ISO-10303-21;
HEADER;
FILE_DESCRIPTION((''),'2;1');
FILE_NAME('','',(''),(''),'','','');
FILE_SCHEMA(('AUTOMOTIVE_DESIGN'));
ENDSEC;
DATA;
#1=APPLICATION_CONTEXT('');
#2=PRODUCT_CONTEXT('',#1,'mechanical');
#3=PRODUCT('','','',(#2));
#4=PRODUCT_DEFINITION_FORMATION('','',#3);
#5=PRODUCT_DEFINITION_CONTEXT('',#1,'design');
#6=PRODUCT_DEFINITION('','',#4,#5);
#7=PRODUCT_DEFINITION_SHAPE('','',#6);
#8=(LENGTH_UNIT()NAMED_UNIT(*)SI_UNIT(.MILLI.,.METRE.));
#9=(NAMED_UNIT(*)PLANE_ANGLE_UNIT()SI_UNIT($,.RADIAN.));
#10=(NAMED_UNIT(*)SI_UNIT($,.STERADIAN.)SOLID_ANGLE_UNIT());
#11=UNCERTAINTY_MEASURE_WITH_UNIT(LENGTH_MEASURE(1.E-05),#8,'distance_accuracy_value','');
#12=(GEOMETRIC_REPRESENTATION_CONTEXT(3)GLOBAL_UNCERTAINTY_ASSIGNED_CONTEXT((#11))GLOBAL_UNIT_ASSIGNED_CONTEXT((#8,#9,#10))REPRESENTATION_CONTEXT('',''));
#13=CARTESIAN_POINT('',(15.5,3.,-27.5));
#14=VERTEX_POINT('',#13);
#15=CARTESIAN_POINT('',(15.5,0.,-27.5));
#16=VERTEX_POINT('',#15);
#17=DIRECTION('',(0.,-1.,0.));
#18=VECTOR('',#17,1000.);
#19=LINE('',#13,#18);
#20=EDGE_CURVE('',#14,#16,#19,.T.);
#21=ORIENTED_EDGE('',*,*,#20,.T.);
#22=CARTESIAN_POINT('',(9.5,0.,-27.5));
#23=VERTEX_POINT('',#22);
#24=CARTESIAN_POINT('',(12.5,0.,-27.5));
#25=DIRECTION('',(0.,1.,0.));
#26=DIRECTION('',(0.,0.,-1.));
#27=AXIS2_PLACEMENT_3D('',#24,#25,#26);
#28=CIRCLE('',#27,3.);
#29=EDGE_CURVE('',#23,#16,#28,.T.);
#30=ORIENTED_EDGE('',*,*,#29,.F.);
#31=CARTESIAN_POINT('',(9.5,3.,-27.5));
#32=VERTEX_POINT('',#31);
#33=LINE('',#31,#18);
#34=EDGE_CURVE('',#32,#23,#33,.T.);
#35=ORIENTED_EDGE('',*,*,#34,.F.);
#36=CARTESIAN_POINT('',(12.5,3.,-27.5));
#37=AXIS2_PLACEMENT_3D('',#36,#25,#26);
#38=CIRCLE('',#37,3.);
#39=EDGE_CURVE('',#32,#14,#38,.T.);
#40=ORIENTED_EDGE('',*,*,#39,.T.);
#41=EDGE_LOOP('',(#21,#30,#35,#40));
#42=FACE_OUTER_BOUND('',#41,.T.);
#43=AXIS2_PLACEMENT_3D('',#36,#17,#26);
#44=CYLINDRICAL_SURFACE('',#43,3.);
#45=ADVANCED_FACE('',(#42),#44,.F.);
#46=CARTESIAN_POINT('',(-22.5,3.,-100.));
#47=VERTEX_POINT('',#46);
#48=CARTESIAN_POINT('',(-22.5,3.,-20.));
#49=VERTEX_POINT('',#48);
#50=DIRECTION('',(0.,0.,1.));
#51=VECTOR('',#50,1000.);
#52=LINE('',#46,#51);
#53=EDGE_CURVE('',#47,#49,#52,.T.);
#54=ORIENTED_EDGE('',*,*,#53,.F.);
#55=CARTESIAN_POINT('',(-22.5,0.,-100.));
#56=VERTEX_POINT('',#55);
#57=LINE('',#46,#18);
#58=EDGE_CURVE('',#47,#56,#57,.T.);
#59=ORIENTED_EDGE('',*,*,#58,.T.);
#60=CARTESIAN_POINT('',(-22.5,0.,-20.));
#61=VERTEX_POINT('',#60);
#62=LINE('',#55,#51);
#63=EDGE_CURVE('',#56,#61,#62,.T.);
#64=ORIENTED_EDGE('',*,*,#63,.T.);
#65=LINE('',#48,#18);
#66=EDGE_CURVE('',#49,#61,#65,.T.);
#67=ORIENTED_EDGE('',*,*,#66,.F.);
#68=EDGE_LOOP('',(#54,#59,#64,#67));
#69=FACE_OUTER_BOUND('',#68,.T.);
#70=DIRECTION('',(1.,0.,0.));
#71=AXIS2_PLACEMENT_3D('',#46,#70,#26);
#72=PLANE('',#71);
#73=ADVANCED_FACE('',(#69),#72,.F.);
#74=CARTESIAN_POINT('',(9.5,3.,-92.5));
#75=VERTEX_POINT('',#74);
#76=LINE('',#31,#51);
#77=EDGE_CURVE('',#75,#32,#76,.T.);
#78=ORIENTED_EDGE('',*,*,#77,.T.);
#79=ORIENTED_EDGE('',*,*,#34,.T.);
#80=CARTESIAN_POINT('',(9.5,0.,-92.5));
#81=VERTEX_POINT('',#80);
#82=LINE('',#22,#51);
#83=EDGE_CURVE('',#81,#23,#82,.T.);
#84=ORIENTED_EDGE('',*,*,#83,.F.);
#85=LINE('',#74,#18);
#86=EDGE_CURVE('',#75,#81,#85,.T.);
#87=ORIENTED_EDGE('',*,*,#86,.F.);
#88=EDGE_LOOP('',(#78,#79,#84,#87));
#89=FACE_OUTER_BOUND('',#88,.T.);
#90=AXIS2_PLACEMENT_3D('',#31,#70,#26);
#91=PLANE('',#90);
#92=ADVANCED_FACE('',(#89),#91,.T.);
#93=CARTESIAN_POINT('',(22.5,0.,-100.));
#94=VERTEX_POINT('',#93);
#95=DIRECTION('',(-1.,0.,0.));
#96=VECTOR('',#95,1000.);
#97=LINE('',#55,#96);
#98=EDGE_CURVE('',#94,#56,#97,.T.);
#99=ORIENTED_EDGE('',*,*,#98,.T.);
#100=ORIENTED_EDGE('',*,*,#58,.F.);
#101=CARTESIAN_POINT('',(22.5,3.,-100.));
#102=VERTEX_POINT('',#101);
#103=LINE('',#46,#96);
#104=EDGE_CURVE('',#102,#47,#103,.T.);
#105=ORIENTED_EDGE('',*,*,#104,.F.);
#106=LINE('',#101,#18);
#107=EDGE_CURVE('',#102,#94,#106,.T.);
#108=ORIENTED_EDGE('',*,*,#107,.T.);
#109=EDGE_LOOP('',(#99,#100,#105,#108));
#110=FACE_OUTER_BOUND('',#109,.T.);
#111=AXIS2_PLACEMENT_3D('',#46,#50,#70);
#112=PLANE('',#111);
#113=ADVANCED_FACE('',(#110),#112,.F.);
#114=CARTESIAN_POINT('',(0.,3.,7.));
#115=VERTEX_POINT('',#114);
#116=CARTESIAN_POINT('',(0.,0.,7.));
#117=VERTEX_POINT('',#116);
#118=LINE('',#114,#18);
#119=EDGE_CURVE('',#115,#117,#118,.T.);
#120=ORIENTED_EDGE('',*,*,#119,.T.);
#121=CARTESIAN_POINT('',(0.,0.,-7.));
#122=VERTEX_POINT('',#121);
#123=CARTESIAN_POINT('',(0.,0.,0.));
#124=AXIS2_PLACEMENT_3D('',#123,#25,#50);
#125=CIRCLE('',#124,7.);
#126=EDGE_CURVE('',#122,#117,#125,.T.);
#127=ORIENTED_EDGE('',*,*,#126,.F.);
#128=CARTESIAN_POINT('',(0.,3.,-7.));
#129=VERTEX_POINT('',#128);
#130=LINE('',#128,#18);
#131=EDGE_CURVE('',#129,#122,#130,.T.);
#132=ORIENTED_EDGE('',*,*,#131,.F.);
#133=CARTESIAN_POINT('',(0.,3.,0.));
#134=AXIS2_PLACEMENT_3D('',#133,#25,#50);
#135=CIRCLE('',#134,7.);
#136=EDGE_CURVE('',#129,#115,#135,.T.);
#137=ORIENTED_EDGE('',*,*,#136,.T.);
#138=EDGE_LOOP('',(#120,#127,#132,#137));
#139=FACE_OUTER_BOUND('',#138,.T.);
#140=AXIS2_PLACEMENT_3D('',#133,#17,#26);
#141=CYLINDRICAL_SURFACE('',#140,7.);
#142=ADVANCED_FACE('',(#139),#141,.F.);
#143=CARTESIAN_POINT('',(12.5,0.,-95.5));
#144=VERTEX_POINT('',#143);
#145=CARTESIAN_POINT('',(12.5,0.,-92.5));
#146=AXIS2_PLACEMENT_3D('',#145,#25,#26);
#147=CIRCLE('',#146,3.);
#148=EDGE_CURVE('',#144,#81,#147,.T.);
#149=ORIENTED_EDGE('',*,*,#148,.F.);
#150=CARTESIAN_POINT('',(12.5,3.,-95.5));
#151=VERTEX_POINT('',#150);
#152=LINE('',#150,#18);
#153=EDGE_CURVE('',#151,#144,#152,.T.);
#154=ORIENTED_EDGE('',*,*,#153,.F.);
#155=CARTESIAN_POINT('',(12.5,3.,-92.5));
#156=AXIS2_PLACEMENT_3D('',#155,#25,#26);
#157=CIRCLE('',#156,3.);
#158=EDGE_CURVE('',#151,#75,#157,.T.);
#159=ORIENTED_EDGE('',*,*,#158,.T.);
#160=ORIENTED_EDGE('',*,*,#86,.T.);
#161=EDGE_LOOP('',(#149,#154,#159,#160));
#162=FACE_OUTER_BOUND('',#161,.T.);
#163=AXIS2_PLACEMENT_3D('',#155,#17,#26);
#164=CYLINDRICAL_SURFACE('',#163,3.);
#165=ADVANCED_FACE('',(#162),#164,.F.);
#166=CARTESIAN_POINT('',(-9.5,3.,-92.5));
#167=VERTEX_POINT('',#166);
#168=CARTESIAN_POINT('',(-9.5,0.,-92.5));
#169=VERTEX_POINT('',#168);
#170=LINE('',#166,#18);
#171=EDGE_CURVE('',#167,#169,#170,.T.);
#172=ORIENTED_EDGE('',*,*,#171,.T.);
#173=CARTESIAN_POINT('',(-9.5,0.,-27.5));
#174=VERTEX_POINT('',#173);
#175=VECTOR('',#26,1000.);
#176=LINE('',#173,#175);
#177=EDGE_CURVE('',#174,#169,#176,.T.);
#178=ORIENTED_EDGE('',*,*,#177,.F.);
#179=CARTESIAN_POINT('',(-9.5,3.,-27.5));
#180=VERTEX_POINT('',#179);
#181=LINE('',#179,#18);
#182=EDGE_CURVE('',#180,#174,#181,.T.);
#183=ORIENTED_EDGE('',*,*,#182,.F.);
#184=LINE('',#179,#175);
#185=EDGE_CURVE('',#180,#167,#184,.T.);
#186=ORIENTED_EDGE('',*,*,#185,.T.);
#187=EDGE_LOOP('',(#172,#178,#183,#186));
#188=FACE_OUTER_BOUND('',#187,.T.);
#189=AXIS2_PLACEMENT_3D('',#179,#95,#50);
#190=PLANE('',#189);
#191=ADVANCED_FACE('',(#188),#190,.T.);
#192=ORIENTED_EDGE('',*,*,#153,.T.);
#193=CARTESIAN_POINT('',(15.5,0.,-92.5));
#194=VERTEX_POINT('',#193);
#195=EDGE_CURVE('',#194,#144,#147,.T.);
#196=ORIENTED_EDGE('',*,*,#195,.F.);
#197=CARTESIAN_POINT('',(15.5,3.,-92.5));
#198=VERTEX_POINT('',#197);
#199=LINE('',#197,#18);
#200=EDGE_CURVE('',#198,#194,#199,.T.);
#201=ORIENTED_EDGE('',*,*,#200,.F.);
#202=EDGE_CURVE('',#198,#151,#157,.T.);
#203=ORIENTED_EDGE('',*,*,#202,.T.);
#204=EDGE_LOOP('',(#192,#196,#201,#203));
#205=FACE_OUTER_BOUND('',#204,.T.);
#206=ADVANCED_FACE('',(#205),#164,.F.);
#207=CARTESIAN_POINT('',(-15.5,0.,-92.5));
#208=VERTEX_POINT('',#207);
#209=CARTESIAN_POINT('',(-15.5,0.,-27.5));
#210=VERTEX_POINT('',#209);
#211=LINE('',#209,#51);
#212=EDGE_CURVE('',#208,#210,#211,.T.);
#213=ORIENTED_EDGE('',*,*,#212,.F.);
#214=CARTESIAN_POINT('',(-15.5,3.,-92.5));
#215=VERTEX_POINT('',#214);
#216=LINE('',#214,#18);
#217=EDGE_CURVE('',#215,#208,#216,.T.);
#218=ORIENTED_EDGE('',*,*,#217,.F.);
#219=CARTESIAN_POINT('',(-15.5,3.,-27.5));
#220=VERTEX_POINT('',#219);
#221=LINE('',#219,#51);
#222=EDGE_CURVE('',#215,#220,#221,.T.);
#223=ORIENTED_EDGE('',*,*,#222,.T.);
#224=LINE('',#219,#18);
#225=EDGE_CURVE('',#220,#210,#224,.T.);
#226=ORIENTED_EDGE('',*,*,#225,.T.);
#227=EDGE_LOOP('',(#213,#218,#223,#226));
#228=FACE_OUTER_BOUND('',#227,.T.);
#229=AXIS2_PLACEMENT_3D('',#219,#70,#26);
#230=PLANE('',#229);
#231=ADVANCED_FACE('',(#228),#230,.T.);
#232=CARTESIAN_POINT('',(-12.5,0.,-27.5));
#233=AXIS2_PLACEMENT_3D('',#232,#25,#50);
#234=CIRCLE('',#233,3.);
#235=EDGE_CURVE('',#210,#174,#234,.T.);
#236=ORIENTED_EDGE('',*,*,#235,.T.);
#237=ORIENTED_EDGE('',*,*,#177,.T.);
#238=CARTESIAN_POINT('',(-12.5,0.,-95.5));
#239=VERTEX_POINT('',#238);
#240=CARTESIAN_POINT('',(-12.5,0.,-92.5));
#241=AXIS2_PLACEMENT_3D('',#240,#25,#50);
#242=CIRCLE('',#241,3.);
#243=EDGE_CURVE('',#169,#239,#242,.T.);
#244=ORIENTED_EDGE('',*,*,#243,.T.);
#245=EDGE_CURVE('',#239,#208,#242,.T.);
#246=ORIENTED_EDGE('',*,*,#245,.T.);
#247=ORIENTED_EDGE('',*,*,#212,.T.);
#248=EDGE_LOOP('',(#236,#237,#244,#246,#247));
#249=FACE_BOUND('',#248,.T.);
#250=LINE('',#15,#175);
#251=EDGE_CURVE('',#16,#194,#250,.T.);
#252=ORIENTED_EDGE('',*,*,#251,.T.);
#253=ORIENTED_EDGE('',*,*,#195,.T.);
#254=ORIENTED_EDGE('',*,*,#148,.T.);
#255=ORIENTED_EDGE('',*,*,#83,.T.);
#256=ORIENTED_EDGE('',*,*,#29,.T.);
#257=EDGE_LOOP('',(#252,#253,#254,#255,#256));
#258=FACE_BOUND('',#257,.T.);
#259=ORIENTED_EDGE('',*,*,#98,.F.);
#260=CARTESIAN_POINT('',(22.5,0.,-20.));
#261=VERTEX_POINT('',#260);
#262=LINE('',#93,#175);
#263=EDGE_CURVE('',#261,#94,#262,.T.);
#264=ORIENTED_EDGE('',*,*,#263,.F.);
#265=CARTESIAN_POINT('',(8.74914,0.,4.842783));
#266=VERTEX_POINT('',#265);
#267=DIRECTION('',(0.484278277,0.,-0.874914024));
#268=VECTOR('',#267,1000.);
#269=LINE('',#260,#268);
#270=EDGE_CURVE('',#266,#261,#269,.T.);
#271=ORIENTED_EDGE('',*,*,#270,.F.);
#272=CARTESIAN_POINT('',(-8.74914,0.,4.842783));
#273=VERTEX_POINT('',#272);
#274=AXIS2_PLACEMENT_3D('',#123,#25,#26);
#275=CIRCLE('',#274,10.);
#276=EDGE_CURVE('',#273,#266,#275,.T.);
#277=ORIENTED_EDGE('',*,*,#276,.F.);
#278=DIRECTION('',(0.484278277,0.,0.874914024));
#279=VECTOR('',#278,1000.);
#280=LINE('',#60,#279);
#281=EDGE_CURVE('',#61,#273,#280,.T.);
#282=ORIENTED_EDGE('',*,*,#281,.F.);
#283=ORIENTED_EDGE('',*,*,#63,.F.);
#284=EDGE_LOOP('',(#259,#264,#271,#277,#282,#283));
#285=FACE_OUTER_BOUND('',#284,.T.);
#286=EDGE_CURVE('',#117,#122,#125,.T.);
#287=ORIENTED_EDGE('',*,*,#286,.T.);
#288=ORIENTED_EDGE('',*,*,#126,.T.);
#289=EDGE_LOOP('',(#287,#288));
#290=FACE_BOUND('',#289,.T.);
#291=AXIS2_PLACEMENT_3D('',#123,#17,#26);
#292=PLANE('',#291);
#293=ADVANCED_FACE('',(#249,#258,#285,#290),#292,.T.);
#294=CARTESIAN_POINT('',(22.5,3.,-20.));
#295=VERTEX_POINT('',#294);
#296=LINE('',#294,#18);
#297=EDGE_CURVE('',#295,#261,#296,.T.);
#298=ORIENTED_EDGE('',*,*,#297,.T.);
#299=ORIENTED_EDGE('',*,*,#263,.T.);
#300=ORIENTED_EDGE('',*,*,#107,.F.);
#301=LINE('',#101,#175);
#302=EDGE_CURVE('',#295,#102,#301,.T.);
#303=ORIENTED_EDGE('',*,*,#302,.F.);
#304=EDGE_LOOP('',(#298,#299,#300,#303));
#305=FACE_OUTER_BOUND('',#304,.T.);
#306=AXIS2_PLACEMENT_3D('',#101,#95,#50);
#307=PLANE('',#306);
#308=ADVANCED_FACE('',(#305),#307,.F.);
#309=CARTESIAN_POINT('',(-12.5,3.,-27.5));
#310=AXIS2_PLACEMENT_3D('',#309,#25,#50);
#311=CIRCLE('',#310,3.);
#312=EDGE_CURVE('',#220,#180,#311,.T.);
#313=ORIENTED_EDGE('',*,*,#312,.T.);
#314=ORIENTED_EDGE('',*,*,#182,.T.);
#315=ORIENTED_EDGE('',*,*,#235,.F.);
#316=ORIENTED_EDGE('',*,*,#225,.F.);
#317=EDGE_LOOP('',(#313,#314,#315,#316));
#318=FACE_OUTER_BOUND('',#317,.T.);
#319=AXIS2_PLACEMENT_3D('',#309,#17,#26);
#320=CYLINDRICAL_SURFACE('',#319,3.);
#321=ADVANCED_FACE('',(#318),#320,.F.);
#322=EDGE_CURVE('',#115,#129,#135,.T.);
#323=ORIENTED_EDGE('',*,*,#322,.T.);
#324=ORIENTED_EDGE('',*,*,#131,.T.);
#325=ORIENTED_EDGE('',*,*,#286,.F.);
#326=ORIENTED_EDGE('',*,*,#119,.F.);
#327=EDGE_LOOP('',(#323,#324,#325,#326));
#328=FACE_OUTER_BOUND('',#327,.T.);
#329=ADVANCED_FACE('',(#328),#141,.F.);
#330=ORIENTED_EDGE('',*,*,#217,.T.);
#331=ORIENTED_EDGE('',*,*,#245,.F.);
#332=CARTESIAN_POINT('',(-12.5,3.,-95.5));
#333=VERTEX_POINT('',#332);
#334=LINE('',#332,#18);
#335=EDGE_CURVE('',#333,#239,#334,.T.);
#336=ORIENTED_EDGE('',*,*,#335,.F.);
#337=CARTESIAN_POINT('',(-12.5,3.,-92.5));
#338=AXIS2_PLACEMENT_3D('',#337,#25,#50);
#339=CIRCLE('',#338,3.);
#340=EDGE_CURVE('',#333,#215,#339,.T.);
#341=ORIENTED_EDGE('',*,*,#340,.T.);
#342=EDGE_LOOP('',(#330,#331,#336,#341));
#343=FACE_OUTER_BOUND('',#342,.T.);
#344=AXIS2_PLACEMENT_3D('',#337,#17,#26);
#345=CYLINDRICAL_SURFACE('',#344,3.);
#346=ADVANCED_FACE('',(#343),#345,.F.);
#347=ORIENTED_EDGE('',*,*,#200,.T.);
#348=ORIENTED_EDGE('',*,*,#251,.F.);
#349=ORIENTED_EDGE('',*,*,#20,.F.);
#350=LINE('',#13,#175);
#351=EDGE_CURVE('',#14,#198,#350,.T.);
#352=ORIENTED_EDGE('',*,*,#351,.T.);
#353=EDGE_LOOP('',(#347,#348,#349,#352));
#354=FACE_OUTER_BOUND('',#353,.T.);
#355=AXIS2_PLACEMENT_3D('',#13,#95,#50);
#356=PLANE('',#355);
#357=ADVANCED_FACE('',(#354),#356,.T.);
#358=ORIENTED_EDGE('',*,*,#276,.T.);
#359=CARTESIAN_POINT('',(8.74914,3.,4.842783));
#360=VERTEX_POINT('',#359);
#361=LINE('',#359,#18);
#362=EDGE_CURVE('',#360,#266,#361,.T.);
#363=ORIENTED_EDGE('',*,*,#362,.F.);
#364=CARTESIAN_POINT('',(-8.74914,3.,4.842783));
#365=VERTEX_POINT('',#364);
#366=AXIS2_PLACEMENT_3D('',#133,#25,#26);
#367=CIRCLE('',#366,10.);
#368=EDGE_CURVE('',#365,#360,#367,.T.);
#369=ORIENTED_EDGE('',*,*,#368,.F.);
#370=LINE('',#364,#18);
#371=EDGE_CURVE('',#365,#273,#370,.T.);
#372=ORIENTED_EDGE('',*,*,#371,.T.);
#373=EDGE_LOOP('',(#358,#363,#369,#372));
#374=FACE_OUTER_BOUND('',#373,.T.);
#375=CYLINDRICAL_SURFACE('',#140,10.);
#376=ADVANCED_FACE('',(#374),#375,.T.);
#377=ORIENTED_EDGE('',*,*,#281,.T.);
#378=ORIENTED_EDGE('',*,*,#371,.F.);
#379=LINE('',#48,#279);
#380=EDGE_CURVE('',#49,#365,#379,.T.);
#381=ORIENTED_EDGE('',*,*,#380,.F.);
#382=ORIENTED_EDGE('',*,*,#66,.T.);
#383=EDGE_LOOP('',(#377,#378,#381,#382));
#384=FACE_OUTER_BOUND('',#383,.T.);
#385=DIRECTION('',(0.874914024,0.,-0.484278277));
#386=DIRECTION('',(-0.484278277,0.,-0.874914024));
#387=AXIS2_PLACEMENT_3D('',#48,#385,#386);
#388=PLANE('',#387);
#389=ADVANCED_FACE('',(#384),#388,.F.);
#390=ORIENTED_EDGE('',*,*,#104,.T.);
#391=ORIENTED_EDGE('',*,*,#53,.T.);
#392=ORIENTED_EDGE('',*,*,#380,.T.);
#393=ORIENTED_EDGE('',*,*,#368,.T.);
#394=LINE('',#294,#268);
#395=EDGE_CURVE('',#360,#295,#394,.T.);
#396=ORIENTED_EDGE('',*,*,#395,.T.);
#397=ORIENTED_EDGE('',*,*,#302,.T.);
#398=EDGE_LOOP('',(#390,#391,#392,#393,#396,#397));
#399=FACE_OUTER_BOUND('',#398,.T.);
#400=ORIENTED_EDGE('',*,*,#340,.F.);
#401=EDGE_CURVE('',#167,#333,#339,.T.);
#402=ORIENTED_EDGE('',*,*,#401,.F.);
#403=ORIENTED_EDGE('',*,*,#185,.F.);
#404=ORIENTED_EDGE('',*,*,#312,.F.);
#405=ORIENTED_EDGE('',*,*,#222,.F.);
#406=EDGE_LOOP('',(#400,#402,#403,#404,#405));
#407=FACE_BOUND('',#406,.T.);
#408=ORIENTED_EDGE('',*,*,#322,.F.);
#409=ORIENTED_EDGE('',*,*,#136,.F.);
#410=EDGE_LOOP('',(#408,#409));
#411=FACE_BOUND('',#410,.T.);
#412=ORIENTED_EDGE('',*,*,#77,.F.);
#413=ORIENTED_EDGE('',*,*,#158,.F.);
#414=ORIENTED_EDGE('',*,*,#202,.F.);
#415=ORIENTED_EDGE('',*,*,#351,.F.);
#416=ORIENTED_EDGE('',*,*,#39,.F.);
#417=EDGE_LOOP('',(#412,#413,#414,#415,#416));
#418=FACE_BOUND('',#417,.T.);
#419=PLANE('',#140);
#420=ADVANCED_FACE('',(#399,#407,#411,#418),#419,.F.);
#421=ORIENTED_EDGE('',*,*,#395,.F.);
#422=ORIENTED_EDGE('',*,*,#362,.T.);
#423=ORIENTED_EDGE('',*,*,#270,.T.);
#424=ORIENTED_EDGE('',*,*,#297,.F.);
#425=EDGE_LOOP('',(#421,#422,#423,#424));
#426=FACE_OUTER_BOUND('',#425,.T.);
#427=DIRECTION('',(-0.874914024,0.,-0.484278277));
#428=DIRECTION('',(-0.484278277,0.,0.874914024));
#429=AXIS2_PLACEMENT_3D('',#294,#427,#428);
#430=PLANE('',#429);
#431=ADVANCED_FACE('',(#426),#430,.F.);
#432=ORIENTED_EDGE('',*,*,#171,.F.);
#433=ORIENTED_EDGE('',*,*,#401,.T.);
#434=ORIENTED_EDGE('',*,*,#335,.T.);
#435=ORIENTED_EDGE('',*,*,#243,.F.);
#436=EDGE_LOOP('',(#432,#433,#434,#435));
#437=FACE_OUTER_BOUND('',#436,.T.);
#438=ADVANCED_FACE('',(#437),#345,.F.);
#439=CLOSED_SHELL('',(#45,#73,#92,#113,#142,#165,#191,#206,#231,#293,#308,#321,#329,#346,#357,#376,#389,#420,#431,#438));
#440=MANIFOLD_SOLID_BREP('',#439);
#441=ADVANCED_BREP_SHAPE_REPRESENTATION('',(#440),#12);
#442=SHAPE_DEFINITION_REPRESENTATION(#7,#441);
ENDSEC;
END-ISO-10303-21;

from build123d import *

# Parameters (mm, degrees)
SKETCH1_R           = 7
BOSS_EXTRUDE1_DEPTH = 3


with BuildPart() as part:
    # Sketch1 → Boss-Extrude1 (new body)
    with BuildSketch(Plane(origin=(0, 0, 0), x_dir=(1, 0, 0), z_dir=(0, 1, 0))):
        with BuildLine():
            Line((-22.5, 100), (22.5, 100))
            Line((22.5, 100), (22.5, 20))
            Line((22.5, 20), (8.749140244, -4.842782774))
            ThreePointArc((8.749140244, -4.842782774), (0, -10), (-8.749140244, -4.842782774))
            Line((-8.749140244, -4.842782774), (-22.5, 20))
            Line((-22.5, 20), (-22.5, 100))
        make_face()
        with Locations(Location((0, 0, 0), (0, 0, 270))):
            Circle(SKETCH1_R, mode=Mode.SUBTRACT)
        with BuildLine():
            Line((-15.5, 27.5), (-15.5, 92.5))
            ThreePointArc((-15.5, 92.5), (-12.5, 95.5), (-9.5, 92.5))
            Line((-9.5, 92.5), (-9.5, 27.5))
            ThreePointArc((-9.5, 27.5), (-12.5, 24.5), (-15.5, 27.5))
        make_face(mode=Mode.SUBTRACT)
        with BuildLine():
            Line((15.5, 27.5), (15.5, 92.5))
            ThreePointArc((15.5, 92.5), (12.5, 95.5), (9.5, 92.5))
            Line((9.5, 92.5), (9.5, 27.5))
            ThreePointArc((9.5, 27.5), (12.5, 24.5), (15.5, 27.5))
        make_face(mode=Mode.SUBTRACT)
    extrude(amount=BOSS_EXTRUDE1_DEPTH)


solid = part.part
